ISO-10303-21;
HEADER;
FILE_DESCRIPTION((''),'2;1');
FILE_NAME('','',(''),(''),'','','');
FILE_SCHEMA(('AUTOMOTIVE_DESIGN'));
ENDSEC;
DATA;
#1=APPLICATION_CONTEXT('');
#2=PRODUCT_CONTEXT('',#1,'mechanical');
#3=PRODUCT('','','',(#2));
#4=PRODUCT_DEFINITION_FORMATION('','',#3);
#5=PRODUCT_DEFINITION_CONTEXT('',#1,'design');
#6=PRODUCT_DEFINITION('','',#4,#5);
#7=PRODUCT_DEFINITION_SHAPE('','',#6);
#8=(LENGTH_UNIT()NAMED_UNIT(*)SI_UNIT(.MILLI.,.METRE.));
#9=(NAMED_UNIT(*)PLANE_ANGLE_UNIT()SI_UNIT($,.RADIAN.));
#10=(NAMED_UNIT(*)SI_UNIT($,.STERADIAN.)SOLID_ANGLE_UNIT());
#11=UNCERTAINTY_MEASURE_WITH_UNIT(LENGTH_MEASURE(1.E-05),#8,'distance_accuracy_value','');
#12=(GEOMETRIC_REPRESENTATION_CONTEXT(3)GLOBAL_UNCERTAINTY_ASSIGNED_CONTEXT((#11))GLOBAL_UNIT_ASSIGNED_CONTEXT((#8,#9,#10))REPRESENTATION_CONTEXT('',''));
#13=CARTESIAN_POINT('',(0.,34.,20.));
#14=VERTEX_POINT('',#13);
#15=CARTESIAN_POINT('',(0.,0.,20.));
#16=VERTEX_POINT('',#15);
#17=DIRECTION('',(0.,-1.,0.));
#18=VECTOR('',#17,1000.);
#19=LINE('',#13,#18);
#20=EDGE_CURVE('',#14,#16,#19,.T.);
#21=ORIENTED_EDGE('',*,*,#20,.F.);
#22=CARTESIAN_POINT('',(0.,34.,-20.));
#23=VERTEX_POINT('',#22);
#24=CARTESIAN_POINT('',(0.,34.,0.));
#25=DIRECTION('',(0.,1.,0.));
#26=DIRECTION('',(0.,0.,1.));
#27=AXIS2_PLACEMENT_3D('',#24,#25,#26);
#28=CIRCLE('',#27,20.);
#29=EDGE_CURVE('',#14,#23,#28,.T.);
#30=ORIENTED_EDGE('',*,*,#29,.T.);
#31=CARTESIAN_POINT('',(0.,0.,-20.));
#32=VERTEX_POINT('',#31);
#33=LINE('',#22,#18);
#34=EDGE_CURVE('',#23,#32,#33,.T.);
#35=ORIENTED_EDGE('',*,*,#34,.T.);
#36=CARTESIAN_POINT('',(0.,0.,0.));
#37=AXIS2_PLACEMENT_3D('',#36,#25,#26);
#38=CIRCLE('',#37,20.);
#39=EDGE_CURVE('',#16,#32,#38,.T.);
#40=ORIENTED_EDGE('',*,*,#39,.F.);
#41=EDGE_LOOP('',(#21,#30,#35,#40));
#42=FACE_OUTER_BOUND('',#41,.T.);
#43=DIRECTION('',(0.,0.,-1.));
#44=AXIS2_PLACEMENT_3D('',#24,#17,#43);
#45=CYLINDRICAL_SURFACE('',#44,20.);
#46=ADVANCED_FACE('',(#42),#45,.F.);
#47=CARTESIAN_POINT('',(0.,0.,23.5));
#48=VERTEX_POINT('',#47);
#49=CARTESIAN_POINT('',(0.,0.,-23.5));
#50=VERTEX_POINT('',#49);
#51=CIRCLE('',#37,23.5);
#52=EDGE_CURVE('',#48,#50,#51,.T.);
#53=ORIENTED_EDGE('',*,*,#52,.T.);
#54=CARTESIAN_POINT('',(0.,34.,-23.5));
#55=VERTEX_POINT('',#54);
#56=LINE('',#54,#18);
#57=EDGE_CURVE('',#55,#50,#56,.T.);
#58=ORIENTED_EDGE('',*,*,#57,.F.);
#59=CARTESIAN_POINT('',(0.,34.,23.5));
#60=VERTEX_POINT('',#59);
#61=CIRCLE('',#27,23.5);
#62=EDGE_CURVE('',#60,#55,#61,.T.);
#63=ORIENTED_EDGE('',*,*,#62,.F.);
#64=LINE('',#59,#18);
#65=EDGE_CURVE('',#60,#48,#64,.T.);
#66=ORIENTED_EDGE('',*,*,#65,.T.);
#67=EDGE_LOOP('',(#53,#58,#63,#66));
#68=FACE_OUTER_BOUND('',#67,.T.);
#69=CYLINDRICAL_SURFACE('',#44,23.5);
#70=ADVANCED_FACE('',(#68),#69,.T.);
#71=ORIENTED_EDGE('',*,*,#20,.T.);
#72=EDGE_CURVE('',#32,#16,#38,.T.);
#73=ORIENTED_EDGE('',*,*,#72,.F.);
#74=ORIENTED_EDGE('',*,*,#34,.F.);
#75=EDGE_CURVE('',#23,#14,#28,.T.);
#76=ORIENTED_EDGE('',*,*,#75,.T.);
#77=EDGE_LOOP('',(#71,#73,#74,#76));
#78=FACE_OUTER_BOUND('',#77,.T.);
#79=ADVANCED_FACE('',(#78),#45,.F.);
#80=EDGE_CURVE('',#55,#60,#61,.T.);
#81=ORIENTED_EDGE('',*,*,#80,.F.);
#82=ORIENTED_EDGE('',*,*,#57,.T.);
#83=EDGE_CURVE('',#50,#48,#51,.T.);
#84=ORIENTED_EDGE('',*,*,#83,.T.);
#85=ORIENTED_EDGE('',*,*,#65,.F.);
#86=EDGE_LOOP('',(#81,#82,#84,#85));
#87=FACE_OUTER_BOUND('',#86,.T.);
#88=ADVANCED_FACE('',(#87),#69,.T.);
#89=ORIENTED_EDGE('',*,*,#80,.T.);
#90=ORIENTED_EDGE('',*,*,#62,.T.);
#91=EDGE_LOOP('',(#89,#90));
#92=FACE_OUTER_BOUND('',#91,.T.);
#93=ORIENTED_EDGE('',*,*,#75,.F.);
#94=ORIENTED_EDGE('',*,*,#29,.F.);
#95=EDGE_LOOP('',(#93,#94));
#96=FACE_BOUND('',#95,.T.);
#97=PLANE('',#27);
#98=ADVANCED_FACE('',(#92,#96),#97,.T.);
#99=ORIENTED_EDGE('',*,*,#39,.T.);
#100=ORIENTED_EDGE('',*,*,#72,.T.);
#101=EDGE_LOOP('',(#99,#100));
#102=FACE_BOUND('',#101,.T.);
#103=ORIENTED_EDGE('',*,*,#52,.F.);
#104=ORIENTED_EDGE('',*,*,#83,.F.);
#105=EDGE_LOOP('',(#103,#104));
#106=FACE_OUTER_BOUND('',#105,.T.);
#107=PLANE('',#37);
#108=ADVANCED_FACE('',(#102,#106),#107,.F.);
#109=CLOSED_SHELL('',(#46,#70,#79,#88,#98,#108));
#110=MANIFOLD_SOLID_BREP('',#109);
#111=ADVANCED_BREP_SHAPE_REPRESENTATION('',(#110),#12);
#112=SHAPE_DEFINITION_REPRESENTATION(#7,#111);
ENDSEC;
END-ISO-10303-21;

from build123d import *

# Parameters (mm, degrees)
SKETCH_1_R      = 23.5
SKETCH_1_R_2    = 20
EXTRUDE_1_DEPTH = 34


with BuildPart() as part:
    # 草图1 → 凸台-拉伸1 (new body)
    with BuildSketch(Plane(origin=(0, 0, 0), x_dir=(1, 0, 0), z_dir=(0, 1, 0))):
        with Locations(Location((0, 0, 0), (0, 0, 270))):
            Circle(SKETCH_1_R)
        with Locations(Location((0, 0, 0), (0, 0, 270))):
            Circle(SKETCH_1_R_2, mode=Mode.SUBTRACT)
    extrude(amount=EXTRUDE_1_DEPTH)


solid = part.part
